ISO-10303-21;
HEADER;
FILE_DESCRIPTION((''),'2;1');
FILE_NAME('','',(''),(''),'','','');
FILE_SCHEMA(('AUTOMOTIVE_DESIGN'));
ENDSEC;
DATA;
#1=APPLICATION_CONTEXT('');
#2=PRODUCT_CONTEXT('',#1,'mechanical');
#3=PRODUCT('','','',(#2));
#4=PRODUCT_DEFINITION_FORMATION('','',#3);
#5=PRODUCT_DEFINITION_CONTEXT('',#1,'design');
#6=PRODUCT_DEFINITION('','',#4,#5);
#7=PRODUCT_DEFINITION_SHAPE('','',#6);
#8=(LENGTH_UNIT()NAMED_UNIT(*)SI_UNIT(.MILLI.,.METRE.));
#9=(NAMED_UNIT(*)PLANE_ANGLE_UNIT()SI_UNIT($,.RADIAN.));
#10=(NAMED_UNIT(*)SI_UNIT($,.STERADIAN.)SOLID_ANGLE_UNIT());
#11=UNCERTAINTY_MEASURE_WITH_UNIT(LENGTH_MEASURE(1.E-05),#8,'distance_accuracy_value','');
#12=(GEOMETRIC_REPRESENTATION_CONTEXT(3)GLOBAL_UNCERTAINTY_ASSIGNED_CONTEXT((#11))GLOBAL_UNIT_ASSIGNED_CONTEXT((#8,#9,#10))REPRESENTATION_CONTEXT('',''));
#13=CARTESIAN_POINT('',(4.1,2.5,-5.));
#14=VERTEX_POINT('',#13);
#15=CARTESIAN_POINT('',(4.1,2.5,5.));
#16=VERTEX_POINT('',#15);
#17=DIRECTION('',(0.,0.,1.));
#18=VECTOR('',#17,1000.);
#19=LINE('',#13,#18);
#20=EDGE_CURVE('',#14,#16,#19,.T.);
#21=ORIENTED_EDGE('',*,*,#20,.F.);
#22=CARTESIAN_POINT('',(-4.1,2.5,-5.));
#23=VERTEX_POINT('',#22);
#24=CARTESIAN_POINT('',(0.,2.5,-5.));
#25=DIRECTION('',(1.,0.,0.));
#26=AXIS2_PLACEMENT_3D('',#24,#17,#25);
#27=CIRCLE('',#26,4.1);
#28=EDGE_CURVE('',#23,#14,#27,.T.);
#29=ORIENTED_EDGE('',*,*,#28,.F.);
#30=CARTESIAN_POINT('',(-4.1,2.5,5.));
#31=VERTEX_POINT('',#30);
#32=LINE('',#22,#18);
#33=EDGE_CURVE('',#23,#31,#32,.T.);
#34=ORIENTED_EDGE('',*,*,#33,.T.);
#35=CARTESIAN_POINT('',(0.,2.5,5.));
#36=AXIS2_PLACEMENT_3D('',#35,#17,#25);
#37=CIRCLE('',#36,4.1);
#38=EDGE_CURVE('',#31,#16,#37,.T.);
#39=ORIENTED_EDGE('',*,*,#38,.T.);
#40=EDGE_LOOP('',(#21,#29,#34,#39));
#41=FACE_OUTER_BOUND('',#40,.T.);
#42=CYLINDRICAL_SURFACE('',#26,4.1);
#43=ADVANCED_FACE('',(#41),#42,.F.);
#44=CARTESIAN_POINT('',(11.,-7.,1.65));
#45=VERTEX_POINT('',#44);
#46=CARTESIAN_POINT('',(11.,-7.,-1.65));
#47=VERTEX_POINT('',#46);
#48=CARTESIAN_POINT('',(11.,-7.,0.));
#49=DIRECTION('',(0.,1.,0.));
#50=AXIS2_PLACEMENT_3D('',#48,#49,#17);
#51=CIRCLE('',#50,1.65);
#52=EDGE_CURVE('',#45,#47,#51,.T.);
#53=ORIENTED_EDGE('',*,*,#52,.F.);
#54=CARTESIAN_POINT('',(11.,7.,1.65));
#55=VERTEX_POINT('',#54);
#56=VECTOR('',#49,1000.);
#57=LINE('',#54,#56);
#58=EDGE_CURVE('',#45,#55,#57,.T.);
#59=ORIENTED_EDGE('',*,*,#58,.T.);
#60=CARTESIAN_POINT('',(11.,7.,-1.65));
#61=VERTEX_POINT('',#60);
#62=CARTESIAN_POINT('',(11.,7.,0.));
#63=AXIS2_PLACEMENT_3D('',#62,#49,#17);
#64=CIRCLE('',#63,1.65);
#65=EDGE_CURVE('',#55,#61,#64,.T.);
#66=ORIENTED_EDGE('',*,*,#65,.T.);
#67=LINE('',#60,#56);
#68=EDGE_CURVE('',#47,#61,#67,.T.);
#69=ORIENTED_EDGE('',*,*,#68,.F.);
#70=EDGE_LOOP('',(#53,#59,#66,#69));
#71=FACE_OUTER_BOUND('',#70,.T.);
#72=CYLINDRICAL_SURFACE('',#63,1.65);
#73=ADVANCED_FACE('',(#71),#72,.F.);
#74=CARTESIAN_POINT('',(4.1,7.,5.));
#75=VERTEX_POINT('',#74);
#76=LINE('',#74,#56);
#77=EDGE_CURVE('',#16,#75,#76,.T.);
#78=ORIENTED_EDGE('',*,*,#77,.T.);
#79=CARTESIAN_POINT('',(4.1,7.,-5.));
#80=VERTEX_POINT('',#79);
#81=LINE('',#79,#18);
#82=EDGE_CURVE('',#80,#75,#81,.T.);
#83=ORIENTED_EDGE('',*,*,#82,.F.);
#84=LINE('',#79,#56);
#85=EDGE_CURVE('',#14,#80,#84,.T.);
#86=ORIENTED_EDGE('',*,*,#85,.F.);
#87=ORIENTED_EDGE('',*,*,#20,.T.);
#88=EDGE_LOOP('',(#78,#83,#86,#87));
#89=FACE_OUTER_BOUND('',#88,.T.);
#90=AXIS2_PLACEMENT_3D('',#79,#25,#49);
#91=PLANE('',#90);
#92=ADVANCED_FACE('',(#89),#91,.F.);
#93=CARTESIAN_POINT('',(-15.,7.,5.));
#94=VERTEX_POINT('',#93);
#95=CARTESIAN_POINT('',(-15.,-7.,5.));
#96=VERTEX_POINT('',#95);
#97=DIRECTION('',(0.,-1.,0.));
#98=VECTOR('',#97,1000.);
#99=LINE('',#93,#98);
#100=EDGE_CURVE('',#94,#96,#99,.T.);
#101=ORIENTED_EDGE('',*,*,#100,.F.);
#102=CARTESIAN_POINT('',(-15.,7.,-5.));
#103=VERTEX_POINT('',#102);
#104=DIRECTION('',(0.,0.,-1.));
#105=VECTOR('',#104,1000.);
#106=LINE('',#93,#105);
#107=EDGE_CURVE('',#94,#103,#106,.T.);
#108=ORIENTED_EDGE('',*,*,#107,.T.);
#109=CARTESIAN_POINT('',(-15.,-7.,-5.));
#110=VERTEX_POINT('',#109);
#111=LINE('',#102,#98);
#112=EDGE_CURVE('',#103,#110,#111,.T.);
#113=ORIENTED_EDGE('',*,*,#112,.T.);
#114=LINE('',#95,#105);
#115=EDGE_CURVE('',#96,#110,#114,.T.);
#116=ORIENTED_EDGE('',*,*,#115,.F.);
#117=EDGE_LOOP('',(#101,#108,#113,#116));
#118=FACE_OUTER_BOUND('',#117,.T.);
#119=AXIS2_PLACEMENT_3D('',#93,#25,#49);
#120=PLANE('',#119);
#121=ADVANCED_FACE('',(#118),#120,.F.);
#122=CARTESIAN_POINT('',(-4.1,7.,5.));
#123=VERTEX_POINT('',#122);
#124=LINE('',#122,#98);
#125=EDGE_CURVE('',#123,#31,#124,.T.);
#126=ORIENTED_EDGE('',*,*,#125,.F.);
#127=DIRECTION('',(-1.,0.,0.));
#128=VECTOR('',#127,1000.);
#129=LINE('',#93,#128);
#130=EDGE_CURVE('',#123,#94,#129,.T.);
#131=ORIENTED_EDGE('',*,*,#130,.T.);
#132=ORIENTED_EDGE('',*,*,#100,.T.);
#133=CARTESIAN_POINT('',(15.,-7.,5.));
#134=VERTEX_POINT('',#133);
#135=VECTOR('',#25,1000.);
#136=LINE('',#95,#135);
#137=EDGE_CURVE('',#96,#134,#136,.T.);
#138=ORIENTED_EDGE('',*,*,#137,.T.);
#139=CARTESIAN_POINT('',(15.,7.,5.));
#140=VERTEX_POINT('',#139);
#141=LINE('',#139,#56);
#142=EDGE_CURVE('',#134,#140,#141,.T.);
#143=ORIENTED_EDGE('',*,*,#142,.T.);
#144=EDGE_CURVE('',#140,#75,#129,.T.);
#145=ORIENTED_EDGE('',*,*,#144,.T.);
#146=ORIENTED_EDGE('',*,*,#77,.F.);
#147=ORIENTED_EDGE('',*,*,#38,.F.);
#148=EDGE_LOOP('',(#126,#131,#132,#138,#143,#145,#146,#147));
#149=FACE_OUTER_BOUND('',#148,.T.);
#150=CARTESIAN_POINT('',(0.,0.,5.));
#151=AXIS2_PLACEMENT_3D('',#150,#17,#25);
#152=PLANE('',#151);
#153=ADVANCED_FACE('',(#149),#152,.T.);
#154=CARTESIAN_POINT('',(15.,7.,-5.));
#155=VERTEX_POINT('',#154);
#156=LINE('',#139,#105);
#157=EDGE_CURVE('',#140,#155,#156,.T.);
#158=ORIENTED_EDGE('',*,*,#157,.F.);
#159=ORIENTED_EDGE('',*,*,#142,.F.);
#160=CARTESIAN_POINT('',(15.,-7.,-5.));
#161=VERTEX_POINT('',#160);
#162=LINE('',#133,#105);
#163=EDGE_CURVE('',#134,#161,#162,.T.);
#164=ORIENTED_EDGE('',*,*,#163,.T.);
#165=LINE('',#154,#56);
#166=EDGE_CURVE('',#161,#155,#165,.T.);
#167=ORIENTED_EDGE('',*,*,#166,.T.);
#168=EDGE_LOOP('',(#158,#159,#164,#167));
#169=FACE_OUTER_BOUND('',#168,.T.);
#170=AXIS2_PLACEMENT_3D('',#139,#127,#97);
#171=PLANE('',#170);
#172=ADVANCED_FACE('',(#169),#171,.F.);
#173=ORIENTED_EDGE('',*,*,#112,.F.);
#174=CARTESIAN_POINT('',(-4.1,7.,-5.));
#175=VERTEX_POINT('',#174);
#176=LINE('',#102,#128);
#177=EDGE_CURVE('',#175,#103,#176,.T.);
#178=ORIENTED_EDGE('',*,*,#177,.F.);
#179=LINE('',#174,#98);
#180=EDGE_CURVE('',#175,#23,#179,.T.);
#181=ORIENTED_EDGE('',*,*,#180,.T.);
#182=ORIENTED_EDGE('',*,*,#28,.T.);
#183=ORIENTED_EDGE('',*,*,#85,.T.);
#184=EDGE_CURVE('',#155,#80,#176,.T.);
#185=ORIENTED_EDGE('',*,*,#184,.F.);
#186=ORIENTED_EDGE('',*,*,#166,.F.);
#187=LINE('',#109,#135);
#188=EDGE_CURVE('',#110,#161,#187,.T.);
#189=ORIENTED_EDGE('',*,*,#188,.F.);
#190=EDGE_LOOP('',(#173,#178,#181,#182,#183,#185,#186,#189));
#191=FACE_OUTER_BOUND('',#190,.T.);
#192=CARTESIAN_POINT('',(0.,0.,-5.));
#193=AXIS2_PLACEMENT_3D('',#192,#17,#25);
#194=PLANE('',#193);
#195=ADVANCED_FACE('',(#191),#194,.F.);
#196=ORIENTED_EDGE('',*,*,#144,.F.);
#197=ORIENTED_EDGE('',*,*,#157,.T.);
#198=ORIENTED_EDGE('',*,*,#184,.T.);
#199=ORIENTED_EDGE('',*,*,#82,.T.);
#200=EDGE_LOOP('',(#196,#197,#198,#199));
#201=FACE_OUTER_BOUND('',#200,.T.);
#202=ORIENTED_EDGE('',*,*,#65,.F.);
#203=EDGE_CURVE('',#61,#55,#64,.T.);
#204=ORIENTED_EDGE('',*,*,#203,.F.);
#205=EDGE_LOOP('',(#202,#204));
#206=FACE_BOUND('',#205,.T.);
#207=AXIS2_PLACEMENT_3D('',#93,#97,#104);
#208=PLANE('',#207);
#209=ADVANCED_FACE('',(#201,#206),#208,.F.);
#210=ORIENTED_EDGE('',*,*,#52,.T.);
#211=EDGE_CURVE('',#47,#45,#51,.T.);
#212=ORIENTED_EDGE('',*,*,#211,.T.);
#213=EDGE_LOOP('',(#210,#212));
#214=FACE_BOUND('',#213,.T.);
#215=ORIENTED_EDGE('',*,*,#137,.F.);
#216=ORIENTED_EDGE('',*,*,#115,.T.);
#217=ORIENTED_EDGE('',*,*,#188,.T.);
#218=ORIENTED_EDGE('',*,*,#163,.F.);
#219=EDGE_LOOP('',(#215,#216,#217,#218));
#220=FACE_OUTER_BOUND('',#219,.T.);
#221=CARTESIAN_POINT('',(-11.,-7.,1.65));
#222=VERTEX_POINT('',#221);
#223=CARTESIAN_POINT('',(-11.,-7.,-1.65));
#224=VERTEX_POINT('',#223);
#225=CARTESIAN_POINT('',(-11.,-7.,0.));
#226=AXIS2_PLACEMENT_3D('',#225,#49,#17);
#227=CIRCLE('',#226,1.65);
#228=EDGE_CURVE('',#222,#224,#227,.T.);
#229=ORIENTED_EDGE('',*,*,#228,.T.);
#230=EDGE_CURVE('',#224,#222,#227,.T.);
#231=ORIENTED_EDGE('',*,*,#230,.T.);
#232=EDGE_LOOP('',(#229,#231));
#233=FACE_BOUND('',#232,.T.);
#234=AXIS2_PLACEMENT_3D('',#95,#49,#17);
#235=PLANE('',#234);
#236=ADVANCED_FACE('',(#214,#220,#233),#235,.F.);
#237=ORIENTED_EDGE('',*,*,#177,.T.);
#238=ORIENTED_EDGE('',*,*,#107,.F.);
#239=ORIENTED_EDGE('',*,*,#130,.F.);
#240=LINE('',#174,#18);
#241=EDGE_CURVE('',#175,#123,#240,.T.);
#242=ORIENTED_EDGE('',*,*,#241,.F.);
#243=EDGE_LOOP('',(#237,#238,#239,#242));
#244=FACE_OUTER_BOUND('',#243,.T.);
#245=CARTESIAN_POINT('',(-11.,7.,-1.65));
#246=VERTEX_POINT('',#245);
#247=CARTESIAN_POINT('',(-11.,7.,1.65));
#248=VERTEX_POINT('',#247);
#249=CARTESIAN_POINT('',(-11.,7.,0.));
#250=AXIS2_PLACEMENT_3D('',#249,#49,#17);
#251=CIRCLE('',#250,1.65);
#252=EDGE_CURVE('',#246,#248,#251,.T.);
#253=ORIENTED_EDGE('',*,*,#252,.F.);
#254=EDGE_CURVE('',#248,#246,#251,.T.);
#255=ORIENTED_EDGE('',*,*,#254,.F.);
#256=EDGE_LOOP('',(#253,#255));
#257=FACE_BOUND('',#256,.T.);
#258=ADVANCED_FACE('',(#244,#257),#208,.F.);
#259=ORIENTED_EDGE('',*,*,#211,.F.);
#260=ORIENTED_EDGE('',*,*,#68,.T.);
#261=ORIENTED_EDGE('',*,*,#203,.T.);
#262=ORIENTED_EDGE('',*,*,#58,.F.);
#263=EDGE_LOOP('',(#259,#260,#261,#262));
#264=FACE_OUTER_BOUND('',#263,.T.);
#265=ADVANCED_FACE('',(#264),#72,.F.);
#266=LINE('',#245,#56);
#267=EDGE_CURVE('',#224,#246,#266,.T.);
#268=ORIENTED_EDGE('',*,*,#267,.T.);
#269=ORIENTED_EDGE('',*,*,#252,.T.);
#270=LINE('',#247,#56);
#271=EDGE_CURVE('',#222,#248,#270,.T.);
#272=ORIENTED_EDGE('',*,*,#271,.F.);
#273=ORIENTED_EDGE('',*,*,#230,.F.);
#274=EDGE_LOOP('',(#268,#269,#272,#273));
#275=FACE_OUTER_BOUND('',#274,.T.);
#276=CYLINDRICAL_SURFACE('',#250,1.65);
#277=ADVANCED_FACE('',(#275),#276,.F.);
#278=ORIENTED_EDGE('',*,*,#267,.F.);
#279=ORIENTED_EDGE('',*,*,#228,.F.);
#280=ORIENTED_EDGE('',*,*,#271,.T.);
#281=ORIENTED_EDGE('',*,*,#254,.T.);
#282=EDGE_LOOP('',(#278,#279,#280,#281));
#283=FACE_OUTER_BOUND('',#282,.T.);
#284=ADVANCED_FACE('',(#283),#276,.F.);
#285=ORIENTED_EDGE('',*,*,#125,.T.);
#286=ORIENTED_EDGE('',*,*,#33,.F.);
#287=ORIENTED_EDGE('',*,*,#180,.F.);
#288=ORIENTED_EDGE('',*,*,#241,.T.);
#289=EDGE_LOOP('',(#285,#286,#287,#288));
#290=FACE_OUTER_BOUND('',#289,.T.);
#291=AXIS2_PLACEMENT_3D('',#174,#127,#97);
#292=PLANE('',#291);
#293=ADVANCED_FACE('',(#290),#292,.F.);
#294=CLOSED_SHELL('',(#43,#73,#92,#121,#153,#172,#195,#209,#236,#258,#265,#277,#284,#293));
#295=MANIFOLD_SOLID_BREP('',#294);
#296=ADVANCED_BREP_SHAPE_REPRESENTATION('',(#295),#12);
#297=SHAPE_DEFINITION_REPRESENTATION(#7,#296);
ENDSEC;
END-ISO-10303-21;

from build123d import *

# Parameters (mm, degrees)
SKETCH1_W           = 30
SKETCH1_H           = 14
BOSS_EXTRUDE1_DEPTH = 5
CUT_EXTRUDE1_DEPTH  = 20.339079606
M4_TAPPED_HOLE1_D   = 3.3


with BuildPart() as part:
    # Sketch1 → Boss-Extrude1 (new, symmetric)
    with BuildSketch(Plane.XY):
        Rectangle(SKETCH1_W, SKETCH1_H)
    extrude(amount=BOSS_EXTRUDE1_DEPTH, both=True)

    # Sketch2 → Cut-Extrude1 (cut, through all)
    with BuildSketch(Plane.XY.offset(5)):
        with BuildLine():
            Line((4.1, 7), (4.1, 2.5))
            ThreePointArc((4.1, 2.5), (0, -1.6), (-4.1, 2.5))
            Line((-4.1, 2.5), (-4.1, 7))
            ThreePointArc((-4.1, 7), (0, 11.1), (4.1, 7))
        make_face()
    extrude(amount=-CUT_EXTRUDE1_DEPTH, mode=Mode.SUBTRACT)

    # M4 Tapped Hole1 (through all)
    with Locations(Plane(origin=(0, 7, 0), x_dir=(1, 0, 0), z_dir=(0, 1, 0))):
        with Locations((-11, 0), (11, 0)):
            Hole(M4_TAPPED_HOLE1_D / 2)


solid = part.part
